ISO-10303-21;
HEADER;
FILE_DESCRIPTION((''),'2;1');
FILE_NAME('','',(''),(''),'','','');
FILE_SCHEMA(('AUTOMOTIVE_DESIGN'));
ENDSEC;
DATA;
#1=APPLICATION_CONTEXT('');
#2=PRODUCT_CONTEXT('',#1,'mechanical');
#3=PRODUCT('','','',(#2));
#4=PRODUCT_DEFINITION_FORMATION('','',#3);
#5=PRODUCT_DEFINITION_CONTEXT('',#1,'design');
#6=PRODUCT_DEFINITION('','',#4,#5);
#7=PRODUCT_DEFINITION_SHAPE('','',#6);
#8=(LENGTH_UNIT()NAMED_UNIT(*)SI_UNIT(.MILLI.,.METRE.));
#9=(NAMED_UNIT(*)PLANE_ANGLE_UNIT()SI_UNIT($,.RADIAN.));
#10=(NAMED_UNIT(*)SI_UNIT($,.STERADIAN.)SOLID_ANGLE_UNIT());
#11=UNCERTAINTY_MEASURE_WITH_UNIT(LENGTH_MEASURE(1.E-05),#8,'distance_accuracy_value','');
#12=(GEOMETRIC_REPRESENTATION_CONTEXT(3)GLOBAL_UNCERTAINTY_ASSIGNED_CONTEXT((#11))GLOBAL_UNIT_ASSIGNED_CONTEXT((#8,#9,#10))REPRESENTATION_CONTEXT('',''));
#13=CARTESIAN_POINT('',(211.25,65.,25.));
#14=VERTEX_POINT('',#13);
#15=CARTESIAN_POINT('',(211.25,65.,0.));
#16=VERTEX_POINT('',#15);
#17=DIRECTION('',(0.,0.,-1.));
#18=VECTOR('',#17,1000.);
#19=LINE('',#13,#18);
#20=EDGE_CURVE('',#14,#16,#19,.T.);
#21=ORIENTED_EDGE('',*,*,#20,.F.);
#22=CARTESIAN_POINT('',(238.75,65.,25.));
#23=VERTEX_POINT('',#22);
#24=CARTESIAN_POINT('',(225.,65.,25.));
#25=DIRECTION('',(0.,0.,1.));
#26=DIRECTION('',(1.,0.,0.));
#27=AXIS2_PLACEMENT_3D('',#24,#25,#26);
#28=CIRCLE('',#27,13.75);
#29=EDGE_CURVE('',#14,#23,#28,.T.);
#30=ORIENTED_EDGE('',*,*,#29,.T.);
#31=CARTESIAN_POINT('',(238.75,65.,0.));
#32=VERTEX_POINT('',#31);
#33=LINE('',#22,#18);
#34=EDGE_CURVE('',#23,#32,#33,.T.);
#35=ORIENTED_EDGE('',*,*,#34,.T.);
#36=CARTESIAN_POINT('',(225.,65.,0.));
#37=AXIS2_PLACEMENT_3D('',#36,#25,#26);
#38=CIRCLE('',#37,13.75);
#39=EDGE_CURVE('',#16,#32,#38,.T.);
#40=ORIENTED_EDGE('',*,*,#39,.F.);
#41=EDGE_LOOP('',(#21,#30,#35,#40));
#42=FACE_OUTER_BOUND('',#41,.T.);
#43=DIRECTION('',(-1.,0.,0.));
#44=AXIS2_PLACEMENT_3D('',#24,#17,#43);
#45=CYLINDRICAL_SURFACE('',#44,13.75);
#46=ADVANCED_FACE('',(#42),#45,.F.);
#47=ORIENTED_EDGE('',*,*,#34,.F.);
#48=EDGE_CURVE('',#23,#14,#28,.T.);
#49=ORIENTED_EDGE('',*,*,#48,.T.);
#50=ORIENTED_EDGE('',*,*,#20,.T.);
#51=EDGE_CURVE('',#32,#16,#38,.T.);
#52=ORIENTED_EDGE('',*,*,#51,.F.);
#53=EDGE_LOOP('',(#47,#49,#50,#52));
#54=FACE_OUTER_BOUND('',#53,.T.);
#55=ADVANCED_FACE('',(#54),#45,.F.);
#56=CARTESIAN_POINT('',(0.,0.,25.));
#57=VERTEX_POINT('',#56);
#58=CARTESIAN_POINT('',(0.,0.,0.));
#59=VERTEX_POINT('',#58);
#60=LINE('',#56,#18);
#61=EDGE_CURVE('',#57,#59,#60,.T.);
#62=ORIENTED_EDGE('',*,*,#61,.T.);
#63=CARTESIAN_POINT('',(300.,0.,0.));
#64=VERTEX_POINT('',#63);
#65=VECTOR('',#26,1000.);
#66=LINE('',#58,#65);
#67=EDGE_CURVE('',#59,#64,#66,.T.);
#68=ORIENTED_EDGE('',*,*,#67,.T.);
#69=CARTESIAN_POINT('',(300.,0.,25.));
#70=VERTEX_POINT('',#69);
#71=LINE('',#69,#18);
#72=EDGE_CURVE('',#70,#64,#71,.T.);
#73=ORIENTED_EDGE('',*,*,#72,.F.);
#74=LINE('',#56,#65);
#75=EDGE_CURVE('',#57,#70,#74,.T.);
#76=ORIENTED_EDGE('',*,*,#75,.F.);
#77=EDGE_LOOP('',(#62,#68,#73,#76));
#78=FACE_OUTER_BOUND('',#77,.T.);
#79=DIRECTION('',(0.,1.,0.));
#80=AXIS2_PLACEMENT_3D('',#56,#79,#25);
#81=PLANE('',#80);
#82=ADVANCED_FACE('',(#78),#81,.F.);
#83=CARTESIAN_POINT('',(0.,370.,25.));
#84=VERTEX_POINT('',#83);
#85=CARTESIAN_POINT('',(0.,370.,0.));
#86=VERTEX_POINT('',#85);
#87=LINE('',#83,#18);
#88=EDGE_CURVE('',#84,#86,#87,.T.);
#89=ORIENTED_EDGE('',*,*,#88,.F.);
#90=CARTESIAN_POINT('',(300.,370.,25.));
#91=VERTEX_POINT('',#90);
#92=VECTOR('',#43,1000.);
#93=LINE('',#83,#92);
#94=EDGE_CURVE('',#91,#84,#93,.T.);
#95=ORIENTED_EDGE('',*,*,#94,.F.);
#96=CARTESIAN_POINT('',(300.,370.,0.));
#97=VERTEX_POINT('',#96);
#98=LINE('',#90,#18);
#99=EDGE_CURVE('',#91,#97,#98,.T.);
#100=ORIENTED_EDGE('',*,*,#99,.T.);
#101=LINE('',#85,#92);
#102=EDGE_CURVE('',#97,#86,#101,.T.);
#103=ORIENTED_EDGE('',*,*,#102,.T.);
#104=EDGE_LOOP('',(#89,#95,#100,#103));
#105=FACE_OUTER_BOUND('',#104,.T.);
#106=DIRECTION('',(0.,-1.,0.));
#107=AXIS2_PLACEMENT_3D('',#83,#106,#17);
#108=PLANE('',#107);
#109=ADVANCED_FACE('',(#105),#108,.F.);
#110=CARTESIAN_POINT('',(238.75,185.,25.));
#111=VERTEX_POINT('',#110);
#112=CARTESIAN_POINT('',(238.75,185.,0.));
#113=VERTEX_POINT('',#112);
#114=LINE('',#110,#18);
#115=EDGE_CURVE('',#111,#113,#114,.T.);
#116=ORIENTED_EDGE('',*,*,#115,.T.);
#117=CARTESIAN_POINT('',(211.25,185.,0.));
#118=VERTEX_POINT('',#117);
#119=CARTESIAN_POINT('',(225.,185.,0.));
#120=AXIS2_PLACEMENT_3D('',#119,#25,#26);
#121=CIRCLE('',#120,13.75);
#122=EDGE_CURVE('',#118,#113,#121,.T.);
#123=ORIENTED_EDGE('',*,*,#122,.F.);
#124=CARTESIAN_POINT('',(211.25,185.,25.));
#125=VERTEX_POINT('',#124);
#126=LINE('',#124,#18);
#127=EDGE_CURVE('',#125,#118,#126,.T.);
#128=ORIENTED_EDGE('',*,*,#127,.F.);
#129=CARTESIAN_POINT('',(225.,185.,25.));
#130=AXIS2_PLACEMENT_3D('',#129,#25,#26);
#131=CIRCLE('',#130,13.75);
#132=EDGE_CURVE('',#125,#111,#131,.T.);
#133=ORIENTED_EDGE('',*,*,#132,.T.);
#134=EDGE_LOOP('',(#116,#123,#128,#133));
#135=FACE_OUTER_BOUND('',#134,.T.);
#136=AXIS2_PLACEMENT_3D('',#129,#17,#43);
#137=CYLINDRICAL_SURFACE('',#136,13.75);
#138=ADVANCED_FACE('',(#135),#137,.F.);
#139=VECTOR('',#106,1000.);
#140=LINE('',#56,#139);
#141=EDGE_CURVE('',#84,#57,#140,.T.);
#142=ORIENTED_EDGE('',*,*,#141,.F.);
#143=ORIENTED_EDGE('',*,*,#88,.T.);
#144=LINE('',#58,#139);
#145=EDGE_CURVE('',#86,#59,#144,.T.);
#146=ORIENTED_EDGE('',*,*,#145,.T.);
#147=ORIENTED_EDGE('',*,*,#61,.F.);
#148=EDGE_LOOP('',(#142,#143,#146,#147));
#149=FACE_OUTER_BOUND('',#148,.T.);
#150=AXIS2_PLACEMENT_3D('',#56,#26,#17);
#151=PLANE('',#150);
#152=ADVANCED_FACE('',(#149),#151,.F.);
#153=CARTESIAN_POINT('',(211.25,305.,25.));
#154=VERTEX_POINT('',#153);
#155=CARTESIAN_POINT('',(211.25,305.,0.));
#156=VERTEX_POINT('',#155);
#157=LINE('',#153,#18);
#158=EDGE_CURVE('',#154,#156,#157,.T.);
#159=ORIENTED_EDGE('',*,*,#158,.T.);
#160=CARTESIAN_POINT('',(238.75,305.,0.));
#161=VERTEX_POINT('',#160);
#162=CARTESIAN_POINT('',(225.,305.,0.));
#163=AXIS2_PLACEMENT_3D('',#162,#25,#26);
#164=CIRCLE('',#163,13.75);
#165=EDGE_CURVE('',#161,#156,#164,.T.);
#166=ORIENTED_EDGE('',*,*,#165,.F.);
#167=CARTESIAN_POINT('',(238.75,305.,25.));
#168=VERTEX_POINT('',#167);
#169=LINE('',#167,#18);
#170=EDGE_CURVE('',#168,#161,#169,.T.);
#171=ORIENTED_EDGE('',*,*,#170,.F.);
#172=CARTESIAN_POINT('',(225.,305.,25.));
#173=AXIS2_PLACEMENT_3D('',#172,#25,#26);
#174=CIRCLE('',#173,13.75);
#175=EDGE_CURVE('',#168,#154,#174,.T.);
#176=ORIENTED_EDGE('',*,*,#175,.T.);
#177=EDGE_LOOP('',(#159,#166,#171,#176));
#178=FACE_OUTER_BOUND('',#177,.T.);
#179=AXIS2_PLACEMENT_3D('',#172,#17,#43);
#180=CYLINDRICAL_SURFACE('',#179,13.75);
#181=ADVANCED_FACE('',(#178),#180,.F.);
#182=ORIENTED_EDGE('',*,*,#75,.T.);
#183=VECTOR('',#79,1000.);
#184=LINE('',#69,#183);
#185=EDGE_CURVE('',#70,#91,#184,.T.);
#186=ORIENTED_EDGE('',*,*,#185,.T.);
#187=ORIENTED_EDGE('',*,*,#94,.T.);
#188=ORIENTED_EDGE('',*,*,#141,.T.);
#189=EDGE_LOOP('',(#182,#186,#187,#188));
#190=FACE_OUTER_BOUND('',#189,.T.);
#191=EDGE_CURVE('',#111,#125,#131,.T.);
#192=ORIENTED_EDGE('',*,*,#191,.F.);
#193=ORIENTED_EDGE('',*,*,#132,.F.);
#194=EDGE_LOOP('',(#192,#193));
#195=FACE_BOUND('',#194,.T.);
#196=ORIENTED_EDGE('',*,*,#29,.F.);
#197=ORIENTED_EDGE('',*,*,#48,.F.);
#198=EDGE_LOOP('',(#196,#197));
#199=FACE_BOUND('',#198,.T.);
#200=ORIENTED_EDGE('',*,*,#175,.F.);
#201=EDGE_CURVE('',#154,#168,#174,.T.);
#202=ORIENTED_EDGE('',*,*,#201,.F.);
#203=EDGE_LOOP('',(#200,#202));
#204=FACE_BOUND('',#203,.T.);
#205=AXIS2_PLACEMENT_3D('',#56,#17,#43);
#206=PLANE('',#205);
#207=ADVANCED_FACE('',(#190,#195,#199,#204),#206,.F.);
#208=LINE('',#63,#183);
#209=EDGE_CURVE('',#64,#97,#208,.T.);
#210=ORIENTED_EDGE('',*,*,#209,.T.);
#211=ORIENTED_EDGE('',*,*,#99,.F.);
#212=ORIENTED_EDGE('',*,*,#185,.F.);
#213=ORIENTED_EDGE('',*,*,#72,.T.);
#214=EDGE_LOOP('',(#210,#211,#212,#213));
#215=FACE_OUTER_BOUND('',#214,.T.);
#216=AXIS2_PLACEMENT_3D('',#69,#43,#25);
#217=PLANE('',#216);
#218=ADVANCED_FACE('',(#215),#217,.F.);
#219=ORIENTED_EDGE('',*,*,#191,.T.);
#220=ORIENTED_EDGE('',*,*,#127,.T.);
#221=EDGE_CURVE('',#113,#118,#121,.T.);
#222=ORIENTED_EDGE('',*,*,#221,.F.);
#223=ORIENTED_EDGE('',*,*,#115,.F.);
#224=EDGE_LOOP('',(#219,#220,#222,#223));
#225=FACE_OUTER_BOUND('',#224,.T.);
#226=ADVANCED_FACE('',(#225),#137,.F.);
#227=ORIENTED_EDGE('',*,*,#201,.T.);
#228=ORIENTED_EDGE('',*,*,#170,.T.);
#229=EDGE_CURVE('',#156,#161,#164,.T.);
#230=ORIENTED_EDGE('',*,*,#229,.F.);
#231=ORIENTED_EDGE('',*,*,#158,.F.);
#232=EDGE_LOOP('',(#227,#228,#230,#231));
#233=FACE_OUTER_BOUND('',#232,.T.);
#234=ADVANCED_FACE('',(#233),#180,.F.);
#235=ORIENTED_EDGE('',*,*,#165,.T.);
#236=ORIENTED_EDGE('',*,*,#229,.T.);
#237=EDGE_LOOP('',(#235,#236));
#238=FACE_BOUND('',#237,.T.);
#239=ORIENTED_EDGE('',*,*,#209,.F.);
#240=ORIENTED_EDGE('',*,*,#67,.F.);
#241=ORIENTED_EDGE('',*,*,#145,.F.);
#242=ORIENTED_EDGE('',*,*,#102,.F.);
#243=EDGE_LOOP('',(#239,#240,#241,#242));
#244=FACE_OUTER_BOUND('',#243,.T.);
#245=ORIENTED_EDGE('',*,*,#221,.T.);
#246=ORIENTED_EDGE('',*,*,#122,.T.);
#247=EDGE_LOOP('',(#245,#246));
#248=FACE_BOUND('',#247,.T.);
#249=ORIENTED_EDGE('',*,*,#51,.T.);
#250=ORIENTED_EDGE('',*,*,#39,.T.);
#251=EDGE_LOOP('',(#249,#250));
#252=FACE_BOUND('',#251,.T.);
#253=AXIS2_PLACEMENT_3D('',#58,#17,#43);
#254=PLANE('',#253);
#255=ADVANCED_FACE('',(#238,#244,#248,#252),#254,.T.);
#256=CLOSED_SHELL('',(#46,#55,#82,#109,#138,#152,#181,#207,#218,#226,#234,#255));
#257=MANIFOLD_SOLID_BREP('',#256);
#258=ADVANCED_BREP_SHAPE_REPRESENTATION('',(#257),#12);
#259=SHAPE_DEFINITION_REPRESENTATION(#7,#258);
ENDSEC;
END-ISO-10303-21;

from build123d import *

# Parameters (mm, degrees)
SKETCH1_W           = 300
SKETCH1_H           = 370
SKETCH1_R           = 13.75
BOSS_EXTRUDE1_DEPTH = 25


with BuildPart() as part:
    # Sketch1 → Boss-Extrude1 (new body)
    with BuildSketch(Plane.XY):
        with Locations((150, 185)):
            Rectangle(SKETCH1_W, SKETCH1_H)
        with Locations((225, 305)):
            Circle(SKETCH1_R, mode=Mode.SUBTRACT)
        with Locations((225, 185)):
            Circle(SKETCH1_R, mode=Mode.SUBTRACT)
        with Locations((225, 65)):
            Circle(SKETCH1_R, mode=Mode.SUBTRACT)
    extrude(amount=BOSS_EXTRUDE1_DEPTH)


solid = part.part
